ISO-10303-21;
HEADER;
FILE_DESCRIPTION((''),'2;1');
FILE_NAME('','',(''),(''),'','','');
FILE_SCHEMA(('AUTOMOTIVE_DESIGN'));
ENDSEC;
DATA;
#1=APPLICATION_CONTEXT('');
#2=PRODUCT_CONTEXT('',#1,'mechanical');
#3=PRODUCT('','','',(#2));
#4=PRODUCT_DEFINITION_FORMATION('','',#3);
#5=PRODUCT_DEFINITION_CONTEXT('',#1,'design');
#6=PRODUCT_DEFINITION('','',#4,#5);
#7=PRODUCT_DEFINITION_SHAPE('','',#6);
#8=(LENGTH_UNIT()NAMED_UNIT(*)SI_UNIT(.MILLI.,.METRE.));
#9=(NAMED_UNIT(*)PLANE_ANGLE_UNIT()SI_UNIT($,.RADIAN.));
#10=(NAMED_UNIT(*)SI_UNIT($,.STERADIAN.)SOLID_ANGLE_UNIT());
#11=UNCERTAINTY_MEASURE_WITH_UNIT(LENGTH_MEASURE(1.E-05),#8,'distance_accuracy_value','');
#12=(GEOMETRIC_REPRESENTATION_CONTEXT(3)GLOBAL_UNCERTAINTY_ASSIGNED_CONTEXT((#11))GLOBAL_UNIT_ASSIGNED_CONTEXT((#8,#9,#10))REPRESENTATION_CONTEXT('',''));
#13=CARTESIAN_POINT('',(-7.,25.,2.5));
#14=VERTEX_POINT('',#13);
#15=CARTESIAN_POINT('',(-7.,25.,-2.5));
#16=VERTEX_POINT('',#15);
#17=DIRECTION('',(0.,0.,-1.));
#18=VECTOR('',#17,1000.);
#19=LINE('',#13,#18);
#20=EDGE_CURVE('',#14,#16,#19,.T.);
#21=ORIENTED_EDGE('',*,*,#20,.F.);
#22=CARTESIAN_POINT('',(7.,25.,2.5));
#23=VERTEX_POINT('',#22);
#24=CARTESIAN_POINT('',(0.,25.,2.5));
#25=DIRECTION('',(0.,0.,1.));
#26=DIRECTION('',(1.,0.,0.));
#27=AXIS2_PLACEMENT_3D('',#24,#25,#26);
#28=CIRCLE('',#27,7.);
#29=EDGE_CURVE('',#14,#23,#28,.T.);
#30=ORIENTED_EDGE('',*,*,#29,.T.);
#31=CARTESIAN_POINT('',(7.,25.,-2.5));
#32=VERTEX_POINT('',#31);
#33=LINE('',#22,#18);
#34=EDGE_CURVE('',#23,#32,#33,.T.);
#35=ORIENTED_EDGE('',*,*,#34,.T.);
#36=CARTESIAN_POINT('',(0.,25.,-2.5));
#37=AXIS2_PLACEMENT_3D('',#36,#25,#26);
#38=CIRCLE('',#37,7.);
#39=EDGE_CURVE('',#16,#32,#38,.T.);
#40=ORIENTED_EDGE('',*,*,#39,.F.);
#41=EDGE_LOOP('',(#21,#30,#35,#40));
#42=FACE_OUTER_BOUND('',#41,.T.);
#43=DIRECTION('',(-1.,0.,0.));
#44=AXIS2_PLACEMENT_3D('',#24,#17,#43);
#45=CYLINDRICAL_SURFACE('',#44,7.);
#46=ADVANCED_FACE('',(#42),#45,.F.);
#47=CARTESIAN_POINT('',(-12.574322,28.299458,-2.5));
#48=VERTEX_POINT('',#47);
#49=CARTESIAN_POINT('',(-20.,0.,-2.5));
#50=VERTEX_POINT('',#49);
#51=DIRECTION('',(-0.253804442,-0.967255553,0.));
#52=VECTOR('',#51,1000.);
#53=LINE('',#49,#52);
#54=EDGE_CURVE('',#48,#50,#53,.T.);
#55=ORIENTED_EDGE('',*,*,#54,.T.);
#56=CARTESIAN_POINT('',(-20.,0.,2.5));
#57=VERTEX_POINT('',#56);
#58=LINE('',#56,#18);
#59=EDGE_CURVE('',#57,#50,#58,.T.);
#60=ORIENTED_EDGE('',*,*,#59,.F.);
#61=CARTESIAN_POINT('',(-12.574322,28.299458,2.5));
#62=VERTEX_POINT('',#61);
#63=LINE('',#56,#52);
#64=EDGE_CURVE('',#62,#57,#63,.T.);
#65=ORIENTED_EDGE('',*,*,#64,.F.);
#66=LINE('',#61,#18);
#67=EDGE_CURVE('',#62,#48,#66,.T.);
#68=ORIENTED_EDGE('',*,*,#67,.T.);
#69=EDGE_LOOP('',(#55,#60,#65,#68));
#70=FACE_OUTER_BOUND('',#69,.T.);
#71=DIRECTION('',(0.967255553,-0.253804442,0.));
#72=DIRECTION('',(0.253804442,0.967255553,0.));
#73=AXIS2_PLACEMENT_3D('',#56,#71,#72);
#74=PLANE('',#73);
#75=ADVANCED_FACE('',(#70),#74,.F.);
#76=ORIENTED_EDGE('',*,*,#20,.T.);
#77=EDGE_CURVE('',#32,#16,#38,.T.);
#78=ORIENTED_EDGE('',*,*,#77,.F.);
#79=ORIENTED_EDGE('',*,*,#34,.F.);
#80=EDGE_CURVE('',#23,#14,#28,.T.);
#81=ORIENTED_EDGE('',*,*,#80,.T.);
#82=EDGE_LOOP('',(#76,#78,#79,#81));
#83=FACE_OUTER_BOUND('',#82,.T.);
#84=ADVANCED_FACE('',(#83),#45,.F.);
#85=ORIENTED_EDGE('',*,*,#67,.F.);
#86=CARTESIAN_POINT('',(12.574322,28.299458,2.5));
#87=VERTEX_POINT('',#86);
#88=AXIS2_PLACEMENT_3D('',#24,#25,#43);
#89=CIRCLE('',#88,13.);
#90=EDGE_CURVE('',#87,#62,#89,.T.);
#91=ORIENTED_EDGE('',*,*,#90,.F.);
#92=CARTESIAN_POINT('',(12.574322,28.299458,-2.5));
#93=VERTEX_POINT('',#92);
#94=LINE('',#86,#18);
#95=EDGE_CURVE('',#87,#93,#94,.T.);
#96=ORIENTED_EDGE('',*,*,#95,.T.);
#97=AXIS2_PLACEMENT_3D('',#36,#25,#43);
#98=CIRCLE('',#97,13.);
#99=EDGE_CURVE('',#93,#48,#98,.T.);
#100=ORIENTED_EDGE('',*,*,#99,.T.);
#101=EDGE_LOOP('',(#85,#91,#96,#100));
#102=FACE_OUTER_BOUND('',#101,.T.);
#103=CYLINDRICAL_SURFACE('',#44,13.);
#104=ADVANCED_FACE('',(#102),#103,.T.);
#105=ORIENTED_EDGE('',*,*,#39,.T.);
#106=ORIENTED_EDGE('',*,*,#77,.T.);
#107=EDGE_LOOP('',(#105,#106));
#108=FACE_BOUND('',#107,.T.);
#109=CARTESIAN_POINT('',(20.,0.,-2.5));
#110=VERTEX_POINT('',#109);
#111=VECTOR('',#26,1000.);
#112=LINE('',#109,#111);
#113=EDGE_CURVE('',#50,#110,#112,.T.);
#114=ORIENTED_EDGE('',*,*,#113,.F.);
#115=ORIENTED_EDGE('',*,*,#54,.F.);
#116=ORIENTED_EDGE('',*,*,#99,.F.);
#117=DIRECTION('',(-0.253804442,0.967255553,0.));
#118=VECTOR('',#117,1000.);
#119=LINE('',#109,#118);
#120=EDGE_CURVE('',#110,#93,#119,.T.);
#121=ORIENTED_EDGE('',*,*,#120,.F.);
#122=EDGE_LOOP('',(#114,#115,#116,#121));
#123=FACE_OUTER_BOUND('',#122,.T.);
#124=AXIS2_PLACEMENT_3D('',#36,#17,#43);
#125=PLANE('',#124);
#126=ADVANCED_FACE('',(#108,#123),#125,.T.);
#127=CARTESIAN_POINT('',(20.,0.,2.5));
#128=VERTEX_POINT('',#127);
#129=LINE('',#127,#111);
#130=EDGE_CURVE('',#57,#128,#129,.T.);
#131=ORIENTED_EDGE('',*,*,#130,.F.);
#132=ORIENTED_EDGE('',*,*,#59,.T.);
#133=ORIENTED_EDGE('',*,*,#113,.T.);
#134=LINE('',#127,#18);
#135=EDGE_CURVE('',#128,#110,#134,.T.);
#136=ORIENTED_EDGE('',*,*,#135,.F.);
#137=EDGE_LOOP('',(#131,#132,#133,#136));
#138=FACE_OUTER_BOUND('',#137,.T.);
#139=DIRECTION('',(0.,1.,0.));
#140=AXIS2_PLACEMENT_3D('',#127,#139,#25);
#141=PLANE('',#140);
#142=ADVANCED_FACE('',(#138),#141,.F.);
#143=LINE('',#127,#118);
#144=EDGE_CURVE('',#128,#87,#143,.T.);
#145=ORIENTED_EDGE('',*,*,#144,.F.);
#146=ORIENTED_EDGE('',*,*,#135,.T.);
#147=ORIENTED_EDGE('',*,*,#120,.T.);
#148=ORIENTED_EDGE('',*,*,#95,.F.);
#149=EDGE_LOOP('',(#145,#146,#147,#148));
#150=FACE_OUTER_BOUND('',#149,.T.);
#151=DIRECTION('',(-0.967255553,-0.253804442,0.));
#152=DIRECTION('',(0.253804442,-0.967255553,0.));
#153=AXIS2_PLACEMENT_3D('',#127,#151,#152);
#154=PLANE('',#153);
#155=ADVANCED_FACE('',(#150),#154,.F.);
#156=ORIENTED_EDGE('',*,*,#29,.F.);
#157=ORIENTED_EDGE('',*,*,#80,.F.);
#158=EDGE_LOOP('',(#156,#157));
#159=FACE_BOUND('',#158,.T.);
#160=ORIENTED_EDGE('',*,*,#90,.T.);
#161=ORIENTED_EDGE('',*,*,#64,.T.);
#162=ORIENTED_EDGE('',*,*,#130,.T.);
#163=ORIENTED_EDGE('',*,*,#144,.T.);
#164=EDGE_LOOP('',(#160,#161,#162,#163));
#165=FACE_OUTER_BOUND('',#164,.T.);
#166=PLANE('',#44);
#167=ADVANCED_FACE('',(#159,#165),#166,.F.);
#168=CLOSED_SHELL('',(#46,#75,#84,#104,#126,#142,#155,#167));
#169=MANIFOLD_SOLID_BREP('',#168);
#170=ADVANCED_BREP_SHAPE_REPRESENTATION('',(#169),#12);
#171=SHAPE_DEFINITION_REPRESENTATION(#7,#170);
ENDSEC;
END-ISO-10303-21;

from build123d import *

# Parameters (mm, degrees)
SKETCH1_R           = 7
BOSS_EXTRUDE1_DEPTH = 2.5


with BuildPart() as part:
    # Sketch1 → Boss-Extrude1 (new, symmetric)
    with BuildSketch(Plane.XY):
        with BuildLine():
            Line((20, 0), (-20, 0))
            Line((-20, 0), (-12.57432219, 28.299457752))
            ThreePointArc((-12.57432219, 28.299457752), (0, 38), (12.57432219, 28.299457752))
            Line((12.57432219, 28.299457752), (20, 0))
        make_face()
        with Locations((0, 25)):
            Circle(SKETCH1_R, mode=Mode.SUBTRACT)
    extrude(amount=BOSS_EXTRUDE1_DEPTH, both=True)


solid = part.part
